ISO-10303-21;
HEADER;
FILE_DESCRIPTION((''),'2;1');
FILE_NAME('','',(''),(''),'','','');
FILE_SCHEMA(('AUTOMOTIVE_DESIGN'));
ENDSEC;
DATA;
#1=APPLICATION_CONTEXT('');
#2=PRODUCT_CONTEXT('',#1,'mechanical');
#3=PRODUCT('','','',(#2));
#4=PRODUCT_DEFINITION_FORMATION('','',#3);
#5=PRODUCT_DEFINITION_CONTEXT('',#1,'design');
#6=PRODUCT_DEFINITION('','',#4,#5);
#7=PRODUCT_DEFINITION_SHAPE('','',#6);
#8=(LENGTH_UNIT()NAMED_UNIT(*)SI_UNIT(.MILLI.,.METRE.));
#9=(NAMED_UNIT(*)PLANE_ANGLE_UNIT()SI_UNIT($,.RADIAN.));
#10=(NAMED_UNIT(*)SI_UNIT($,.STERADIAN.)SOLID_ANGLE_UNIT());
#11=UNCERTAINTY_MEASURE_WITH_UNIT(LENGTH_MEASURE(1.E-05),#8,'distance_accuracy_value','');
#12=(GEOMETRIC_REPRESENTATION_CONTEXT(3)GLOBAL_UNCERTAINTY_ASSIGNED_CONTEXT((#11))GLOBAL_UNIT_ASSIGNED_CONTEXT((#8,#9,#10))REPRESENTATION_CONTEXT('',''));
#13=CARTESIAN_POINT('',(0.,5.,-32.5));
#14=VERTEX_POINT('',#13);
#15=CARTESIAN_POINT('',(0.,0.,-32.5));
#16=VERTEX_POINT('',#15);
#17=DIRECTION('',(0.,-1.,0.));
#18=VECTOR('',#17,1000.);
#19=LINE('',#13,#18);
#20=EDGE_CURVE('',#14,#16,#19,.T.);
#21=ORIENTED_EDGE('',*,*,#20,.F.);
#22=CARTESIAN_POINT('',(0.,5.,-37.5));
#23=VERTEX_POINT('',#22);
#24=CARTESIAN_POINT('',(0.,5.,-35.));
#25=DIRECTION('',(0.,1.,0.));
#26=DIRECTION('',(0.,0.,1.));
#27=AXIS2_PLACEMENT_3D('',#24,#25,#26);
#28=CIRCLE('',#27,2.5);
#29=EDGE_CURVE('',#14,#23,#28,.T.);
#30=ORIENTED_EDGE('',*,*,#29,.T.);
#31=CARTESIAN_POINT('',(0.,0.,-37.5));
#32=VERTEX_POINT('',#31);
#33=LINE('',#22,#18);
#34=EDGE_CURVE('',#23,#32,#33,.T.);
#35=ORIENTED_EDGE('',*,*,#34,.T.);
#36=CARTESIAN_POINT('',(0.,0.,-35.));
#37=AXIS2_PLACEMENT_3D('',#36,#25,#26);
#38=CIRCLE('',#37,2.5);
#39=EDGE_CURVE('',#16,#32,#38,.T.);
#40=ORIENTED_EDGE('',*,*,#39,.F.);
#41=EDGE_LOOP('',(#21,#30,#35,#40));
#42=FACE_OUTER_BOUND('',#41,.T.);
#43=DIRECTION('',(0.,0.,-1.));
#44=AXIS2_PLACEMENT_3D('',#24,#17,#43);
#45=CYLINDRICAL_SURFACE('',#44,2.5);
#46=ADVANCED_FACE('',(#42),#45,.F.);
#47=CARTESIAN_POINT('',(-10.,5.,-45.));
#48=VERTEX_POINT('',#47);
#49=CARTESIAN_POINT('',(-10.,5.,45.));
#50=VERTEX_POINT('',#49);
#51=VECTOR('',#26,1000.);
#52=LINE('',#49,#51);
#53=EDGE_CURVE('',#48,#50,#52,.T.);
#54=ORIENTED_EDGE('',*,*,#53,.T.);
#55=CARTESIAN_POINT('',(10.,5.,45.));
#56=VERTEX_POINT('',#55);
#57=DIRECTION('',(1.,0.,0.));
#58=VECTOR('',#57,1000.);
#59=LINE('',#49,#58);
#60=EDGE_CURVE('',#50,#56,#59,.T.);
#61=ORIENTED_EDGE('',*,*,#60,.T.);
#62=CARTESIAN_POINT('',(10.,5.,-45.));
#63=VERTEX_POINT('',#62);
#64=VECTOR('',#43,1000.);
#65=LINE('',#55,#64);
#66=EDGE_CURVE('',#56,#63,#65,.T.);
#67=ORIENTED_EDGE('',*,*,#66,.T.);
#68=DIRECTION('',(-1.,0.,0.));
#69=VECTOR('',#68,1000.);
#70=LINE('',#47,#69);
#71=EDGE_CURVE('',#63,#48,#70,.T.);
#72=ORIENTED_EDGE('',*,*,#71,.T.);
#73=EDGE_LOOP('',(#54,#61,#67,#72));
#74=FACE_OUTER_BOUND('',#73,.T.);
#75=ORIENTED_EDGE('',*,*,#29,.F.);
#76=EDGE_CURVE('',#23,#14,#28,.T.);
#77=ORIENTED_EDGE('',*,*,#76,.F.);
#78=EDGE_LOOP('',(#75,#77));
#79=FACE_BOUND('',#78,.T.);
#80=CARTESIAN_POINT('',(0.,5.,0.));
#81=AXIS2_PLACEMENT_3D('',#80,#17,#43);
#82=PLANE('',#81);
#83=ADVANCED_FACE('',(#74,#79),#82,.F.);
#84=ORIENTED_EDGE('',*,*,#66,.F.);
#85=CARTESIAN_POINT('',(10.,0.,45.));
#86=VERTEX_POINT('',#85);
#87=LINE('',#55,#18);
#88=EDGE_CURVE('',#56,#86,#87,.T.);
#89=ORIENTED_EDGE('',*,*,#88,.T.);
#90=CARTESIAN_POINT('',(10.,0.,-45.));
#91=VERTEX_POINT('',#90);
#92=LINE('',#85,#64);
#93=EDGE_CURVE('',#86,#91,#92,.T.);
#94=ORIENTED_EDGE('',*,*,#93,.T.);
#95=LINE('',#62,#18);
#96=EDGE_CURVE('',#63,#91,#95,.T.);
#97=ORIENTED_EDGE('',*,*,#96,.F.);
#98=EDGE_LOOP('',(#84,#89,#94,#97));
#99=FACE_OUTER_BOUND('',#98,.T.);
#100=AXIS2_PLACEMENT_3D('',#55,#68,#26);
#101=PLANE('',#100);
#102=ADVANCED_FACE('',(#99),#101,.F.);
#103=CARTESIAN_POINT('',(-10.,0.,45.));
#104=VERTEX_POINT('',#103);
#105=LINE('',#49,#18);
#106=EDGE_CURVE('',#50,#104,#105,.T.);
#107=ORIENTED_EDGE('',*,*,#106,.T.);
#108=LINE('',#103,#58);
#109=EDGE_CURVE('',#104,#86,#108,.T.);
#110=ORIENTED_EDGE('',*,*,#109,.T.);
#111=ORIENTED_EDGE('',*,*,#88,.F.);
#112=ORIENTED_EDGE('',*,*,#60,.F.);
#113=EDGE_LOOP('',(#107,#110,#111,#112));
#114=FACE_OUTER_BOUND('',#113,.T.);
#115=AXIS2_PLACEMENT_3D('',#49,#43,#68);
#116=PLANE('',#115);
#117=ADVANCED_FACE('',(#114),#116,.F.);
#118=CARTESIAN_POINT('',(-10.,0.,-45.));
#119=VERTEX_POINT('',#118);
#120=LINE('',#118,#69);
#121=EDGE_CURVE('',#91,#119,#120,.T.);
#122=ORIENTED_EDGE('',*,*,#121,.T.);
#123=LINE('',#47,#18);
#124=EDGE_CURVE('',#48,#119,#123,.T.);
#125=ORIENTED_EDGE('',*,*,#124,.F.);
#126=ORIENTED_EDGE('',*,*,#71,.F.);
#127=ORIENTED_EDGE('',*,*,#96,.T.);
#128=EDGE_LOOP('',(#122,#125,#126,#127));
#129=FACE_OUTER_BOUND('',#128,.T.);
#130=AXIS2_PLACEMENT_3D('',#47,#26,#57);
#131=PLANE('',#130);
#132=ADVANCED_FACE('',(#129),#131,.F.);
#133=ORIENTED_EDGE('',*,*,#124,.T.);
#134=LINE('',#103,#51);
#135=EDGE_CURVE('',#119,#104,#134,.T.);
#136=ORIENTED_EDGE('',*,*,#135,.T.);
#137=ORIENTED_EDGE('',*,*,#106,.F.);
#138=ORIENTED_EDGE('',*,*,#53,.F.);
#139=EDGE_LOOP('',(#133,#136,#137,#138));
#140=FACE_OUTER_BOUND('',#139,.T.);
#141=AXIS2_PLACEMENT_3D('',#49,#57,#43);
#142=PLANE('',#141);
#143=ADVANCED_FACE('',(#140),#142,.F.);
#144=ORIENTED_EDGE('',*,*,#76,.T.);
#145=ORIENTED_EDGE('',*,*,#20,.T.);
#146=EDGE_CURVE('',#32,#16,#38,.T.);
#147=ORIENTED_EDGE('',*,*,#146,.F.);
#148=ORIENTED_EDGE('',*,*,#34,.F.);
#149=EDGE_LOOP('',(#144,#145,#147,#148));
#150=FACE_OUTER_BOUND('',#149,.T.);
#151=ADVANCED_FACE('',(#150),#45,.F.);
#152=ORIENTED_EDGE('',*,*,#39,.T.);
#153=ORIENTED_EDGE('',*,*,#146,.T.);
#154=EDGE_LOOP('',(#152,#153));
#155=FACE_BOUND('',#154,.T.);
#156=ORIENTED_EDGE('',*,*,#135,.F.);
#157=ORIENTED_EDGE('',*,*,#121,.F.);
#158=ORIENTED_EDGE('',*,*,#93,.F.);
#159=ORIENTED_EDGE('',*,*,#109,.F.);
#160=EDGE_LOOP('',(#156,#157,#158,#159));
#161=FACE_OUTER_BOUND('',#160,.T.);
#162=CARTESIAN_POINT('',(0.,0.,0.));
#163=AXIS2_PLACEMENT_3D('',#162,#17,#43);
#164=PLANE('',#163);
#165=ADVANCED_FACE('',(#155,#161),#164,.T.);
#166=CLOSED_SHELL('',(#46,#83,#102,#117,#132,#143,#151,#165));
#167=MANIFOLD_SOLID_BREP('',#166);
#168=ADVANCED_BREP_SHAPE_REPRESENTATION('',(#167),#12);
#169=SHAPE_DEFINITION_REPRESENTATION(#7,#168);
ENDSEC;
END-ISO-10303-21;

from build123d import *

# Parameters (mm, degrees)
SKETCH1_W           = 20
SKETCH1_H           = 90
SKETCH1_R           = 2.5
BOSS_EXTRUDE1_DEPTH = 5


with BuildPart() as part:
    # Sketch1 → Boss-Extrude1 (new body)
    with BuildSketch(Plane(origin=(0, 0, 0), x_dir=(1, 0, 0), z_dir=(0, 1, 0))):
        Rectangle(SKETCH1_W, SKETCH1_H)
        with Locations(Location((0, 35, 0), (0, 0, 270))):
            Circle(SKETCH1_R, mode=Mode.SUBTRACT)
    extrude(amount=BOSS_EXTRUDE1_DEPTH)


solid = part.part
